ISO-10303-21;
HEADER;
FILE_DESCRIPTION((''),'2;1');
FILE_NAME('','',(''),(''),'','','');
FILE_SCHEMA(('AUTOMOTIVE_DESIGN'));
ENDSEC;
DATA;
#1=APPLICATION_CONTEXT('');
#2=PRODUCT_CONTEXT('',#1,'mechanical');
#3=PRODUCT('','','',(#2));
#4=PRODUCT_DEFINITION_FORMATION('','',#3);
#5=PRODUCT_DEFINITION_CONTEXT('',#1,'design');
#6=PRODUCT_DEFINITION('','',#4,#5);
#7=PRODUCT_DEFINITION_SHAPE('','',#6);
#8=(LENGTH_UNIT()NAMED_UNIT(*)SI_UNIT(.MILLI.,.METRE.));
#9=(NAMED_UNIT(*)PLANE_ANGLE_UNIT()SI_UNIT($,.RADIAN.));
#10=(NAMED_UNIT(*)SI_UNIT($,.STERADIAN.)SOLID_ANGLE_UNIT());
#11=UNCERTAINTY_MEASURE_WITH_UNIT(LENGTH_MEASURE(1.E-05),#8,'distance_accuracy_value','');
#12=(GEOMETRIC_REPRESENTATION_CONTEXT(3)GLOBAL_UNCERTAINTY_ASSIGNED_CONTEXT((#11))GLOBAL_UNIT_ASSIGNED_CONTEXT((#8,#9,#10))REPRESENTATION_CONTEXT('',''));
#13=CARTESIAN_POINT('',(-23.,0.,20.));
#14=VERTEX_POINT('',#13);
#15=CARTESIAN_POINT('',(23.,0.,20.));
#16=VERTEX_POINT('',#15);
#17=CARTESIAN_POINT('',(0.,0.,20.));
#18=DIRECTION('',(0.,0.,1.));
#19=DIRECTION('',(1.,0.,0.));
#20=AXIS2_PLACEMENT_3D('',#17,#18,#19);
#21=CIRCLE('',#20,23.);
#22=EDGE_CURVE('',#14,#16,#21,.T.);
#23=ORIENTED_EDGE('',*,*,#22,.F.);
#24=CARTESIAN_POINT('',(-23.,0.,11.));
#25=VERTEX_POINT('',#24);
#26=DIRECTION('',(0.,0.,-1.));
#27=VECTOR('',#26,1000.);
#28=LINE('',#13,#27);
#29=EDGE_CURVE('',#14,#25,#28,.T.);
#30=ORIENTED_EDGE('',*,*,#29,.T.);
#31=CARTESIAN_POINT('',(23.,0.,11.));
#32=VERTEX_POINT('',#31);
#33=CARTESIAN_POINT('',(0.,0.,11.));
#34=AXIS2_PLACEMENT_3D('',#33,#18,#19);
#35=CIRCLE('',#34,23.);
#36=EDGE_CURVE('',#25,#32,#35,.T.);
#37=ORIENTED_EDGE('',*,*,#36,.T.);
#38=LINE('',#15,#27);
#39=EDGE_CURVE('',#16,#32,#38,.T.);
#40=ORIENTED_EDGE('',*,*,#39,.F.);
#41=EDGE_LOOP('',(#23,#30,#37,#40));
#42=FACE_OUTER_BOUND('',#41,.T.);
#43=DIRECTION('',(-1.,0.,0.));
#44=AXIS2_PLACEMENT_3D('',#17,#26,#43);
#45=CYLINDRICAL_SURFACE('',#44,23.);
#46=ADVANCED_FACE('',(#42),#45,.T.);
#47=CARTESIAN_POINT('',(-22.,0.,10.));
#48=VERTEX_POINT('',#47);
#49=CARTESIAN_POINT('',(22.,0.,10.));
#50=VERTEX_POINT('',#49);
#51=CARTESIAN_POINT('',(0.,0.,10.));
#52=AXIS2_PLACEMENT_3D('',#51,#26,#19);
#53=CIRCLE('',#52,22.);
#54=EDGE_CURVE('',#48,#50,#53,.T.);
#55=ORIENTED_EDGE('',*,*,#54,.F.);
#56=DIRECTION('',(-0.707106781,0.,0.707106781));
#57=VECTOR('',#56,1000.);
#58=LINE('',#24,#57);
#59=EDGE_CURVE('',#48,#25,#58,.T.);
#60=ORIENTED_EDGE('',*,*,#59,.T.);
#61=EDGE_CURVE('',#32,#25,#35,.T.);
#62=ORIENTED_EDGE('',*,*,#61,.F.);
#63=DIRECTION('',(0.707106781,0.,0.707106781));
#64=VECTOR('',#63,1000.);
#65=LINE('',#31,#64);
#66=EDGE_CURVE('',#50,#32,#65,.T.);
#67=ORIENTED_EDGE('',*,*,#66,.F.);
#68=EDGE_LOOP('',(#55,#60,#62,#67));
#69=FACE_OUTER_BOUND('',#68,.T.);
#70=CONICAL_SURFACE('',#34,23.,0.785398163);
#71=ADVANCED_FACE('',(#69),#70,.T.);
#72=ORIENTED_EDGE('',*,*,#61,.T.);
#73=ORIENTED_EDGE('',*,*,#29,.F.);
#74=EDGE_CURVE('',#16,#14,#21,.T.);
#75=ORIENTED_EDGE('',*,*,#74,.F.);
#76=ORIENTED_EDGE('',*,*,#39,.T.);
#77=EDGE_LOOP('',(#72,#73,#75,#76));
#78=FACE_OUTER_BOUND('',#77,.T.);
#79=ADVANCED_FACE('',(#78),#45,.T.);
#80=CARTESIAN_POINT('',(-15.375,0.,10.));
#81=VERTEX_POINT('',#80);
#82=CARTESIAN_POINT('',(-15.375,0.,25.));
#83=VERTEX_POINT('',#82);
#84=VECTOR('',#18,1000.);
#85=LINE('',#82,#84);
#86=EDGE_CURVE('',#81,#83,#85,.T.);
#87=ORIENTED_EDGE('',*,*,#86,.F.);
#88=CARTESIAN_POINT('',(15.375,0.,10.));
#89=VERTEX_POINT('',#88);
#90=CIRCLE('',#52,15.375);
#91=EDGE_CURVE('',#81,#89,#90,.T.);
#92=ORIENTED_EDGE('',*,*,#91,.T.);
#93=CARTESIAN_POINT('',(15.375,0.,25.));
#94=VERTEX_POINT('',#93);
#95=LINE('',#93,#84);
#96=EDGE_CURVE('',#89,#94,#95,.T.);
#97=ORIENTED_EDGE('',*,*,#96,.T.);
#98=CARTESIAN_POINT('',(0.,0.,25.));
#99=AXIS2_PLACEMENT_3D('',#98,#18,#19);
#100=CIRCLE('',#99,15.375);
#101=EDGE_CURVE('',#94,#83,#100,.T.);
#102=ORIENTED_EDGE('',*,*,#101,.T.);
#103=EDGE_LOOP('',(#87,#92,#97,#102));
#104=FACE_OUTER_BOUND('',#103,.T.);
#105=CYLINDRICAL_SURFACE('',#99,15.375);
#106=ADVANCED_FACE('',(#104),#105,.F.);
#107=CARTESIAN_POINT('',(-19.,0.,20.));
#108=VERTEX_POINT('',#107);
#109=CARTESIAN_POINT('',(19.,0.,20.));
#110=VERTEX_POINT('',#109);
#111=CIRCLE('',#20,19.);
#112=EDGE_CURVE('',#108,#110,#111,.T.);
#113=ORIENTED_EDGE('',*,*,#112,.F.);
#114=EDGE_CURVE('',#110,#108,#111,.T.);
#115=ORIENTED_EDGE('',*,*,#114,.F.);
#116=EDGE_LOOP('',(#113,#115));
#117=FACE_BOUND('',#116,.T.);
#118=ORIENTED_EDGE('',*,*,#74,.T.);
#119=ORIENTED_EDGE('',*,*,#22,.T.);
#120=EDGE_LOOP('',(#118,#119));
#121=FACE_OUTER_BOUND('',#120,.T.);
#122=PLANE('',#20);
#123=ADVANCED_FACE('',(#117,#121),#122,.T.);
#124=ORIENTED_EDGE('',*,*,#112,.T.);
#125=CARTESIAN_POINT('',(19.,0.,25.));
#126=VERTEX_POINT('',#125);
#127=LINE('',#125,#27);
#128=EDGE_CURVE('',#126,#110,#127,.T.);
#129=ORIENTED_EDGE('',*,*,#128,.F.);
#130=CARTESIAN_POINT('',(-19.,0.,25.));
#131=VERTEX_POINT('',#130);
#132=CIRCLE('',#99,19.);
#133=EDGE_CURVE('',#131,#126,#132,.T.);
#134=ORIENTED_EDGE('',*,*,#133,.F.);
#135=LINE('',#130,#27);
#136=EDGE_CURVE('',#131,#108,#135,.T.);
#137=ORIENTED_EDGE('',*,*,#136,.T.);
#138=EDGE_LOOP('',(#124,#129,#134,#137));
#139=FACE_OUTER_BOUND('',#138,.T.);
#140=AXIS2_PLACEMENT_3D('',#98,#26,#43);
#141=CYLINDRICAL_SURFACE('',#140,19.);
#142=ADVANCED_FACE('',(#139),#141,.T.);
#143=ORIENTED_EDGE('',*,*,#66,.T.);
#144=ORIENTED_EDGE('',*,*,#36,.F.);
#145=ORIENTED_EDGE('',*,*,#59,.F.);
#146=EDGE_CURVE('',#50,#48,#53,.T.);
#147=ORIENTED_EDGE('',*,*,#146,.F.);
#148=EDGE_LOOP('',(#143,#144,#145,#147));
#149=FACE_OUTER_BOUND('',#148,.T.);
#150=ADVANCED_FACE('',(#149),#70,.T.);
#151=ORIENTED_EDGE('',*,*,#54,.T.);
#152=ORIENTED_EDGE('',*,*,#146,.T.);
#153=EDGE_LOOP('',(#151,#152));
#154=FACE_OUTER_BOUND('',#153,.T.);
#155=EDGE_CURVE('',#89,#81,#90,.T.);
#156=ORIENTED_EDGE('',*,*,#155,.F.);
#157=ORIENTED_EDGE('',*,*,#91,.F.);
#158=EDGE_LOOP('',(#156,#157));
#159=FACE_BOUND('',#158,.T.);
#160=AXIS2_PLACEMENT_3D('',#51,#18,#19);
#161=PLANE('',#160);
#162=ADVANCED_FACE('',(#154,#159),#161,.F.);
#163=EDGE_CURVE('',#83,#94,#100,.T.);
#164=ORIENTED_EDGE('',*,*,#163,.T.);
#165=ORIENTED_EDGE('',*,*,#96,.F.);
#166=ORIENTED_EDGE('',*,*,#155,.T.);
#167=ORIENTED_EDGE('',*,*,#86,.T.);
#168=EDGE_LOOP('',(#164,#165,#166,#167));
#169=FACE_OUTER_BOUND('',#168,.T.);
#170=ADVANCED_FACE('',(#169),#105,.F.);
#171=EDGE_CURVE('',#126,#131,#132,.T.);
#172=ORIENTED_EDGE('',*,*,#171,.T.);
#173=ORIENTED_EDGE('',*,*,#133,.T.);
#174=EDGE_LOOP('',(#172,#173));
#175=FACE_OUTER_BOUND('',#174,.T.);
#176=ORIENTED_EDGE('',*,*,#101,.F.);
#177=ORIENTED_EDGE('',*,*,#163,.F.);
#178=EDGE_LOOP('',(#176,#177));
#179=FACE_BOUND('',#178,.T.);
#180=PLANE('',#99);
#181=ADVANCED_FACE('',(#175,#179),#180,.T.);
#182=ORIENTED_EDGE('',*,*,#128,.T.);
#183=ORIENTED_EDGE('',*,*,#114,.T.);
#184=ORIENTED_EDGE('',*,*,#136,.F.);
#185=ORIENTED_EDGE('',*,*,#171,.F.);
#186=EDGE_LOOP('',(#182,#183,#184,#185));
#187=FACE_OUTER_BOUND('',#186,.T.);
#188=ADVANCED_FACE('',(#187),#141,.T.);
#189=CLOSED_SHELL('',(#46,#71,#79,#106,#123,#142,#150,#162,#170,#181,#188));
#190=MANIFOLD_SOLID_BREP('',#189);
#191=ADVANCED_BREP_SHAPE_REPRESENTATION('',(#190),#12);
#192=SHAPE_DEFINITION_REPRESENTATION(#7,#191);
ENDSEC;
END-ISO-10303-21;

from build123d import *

# Parameters (mm, degrees)
SKETCH1_R             = 19
SKETCH1_R_2           = 7.5
BOSS_EXTRUDE1_DEPTH   = 10
SKETCH2_R             = 23
SKETCH2_R_2           = 7.5
BOSS_EXTRUDE2_DEPTH   = 10
SKETCH3_R             = 19
SKETCH3_R_2           = 7.5
BOSS_EXTRUDE3_DEPTH   = 5
G1_TAPPED_HOLE1_D     = 30.75
G1_TAPPED_HOLE1_DEPTH = 73.43
G1_TAPPED_HOLE1_TIP   = 9.238232018
SKETCH6_R             = 28.473904373
CUT_EXTRUDE1_DEPTH    = 10
CHAMFER2_SIZE         = 1


with BuildPart() as part:
    # Sketch1 → Boss-Extrude1 (new body)
    with BuildSketch(Plane.XY):
        Circle(SKETCH1_R)
        Circle(SKETCH1_R_2, mode=Mode.SUBTRACT)
    extrude(amount=BOSS_EXTRUDE1_DEPTH)

    # Sketch2 → Boss-Extrude2 (add)
    with BuildSketch(Plane.XY.offset(10)):
        Circle(SKETCH2_R)
        Circle(SKETCH2_R_2, mode=Mode.SUBTRACT)
    extrude(amount=BOSS_EXTRUDE2_DEPTH)

    # Sketch3 → Boss-Extrude3 (add)
    with BuildSketch(Plane.XY.offset(20)):
        Circle(SKETCH3_R)
        Circle(SKETCH3_R_2, mode=Mode.SUBTRACT)
    extrude(amount=BOSS_EXTRUDE3_DEPTH)

    # G1 Tapped Hole1
    with Locations(Plane.XY.offset(25)):
        with Locations((0, 0)):
            Hole(G1_TAPPED_HOLE1_D / 2, depth=G1_TAPPED_HOLE1_DEPTH)
            with Locations((0, 0, -(G1_TAPPED_HOLE1_DEPTH + G1_TAPPED_HOLE1_TIP / 2))):  # 118° drill point
                Cone(0, G1_TAPPED_HOLE1_D / 2, G1_TAPPED_HOLE1_TIP, mode=Mode.SUBTRACT)

    # Sketch6 → Cut-Extrude1 (cut)
    with BuildSketch(Plane.XY):
        Circle(SKETCH6_R)
    extrude(amount=CUT_EXTRUDE1_DEPTH, mode=Mode.SUBTRACT)

    # Chamfer2
    chamfer2_edges = [part.edges().sort_by_distance(p)[0] for p in [
        (-23, 0, 10),
    ]]
    chamfer(chamfer2_edges, length=CHAMFER2_SIZE)


solid = part.part
